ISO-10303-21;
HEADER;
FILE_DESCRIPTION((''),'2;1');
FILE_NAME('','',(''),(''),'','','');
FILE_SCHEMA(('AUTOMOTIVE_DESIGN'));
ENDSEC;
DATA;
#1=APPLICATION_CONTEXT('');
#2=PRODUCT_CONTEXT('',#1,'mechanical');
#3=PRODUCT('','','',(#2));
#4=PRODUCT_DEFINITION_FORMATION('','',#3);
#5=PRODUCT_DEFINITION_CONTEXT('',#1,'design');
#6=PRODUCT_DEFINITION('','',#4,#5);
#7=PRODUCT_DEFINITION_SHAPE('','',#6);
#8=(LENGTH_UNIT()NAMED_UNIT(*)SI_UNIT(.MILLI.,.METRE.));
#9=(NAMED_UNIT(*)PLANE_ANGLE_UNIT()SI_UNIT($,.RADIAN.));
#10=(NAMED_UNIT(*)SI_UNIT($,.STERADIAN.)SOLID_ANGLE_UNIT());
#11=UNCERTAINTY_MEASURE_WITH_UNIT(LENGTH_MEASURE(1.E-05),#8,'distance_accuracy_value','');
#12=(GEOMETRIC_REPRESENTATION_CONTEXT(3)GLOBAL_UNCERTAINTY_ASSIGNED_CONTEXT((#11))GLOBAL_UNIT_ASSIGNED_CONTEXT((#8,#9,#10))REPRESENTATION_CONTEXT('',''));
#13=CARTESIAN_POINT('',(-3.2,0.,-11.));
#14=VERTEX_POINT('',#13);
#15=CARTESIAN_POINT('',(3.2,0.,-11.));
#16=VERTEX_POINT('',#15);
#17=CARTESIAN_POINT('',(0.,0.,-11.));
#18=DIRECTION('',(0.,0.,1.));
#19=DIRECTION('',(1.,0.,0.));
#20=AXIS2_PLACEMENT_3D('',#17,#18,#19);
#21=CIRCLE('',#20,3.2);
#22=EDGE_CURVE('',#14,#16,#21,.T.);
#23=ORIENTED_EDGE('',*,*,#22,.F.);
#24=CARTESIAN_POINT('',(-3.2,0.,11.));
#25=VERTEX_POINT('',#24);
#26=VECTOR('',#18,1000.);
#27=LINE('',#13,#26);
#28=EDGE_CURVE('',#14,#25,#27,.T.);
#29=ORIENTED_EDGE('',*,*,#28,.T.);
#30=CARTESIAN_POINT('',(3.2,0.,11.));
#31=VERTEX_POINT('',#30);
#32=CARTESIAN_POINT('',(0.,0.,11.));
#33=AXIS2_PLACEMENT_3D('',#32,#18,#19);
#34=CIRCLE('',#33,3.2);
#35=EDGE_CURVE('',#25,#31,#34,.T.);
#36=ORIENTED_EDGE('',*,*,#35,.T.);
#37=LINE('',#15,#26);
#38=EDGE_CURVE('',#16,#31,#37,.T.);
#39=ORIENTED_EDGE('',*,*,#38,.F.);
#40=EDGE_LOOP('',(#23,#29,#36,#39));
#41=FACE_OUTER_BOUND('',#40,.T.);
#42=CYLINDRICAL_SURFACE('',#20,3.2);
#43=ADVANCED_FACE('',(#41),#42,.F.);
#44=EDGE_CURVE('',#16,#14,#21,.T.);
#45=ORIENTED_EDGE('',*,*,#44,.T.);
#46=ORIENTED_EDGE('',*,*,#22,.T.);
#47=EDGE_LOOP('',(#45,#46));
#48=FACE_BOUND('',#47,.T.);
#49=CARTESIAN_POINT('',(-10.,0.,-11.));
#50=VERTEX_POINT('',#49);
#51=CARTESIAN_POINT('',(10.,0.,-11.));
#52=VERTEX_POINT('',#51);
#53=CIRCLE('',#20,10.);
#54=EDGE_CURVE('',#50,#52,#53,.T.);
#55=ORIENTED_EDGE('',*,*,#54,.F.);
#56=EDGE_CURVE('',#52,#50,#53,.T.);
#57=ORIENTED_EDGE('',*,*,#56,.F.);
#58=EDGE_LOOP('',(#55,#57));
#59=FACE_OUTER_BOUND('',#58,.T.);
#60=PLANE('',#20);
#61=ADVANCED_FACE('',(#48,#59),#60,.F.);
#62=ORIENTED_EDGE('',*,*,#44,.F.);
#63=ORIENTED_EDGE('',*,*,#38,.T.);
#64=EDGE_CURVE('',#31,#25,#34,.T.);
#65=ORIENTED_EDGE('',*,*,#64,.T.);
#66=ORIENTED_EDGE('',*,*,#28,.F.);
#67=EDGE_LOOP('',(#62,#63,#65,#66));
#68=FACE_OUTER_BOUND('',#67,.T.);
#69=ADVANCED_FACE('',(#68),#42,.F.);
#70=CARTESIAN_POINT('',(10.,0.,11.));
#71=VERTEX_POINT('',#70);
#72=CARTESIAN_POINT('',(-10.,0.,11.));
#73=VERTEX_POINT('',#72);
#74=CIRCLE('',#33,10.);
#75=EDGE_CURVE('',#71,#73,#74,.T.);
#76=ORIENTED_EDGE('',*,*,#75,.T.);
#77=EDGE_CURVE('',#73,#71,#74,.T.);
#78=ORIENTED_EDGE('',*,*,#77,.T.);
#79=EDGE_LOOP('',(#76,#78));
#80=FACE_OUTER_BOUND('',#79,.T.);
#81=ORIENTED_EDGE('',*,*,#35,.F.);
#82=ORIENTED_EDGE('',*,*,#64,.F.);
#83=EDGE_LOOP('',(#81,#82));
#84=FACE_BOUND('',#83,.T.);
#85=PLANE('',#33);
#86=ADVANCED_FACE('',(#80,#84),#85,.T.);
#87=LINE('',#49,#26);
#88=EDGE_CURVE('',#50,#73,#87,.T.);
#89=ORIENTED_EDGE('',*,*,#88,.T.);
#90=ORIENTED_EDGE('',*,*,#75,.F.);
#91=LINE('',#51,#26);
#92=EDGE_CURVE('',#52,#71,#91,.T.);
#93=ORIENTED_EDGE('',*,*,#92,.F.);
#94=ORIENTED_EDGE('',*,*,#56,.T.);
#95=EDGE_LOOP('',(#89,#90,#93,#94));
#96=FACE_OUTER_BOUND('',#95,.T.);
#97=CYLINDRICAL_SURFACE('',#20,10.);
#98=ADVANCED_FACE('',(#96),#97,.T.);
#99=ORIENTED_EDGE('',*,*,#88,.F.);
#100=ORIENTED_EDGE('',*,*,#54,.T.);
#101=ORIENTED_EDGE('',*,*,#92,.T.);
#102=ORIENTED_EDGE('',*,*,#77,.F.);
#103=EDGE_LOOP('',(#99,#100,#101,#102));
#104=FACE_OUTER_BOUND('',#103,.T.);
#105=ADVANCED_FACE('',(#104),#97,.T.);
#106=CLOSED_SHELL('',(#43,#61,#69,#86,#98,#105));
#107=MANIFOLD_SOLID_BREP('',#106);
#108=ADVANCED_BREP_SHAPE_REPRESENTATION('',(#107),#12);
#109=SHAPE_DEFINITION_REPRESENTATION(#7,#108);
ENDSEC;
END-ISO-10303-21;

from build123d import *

# Parameters (mm, degrees)
SKETCH_1_R      = 10
SKETCH_1_R_2    = 3.2
EXTRUDE_1_DEPTH = 11


with BuildPart() as part:
    # 草图1 → 凸台-拉伸1 (new, symmetric)
    with BuildSketch(Plane.XY):
        Circle(SKETCH_1_R)
        Circle(SKETCH_1_R_2, mode=Mode.SUBTRACT)
    extrude(amount=EXTRUDE_1_DEPTH, both=True)


solid = part.part
